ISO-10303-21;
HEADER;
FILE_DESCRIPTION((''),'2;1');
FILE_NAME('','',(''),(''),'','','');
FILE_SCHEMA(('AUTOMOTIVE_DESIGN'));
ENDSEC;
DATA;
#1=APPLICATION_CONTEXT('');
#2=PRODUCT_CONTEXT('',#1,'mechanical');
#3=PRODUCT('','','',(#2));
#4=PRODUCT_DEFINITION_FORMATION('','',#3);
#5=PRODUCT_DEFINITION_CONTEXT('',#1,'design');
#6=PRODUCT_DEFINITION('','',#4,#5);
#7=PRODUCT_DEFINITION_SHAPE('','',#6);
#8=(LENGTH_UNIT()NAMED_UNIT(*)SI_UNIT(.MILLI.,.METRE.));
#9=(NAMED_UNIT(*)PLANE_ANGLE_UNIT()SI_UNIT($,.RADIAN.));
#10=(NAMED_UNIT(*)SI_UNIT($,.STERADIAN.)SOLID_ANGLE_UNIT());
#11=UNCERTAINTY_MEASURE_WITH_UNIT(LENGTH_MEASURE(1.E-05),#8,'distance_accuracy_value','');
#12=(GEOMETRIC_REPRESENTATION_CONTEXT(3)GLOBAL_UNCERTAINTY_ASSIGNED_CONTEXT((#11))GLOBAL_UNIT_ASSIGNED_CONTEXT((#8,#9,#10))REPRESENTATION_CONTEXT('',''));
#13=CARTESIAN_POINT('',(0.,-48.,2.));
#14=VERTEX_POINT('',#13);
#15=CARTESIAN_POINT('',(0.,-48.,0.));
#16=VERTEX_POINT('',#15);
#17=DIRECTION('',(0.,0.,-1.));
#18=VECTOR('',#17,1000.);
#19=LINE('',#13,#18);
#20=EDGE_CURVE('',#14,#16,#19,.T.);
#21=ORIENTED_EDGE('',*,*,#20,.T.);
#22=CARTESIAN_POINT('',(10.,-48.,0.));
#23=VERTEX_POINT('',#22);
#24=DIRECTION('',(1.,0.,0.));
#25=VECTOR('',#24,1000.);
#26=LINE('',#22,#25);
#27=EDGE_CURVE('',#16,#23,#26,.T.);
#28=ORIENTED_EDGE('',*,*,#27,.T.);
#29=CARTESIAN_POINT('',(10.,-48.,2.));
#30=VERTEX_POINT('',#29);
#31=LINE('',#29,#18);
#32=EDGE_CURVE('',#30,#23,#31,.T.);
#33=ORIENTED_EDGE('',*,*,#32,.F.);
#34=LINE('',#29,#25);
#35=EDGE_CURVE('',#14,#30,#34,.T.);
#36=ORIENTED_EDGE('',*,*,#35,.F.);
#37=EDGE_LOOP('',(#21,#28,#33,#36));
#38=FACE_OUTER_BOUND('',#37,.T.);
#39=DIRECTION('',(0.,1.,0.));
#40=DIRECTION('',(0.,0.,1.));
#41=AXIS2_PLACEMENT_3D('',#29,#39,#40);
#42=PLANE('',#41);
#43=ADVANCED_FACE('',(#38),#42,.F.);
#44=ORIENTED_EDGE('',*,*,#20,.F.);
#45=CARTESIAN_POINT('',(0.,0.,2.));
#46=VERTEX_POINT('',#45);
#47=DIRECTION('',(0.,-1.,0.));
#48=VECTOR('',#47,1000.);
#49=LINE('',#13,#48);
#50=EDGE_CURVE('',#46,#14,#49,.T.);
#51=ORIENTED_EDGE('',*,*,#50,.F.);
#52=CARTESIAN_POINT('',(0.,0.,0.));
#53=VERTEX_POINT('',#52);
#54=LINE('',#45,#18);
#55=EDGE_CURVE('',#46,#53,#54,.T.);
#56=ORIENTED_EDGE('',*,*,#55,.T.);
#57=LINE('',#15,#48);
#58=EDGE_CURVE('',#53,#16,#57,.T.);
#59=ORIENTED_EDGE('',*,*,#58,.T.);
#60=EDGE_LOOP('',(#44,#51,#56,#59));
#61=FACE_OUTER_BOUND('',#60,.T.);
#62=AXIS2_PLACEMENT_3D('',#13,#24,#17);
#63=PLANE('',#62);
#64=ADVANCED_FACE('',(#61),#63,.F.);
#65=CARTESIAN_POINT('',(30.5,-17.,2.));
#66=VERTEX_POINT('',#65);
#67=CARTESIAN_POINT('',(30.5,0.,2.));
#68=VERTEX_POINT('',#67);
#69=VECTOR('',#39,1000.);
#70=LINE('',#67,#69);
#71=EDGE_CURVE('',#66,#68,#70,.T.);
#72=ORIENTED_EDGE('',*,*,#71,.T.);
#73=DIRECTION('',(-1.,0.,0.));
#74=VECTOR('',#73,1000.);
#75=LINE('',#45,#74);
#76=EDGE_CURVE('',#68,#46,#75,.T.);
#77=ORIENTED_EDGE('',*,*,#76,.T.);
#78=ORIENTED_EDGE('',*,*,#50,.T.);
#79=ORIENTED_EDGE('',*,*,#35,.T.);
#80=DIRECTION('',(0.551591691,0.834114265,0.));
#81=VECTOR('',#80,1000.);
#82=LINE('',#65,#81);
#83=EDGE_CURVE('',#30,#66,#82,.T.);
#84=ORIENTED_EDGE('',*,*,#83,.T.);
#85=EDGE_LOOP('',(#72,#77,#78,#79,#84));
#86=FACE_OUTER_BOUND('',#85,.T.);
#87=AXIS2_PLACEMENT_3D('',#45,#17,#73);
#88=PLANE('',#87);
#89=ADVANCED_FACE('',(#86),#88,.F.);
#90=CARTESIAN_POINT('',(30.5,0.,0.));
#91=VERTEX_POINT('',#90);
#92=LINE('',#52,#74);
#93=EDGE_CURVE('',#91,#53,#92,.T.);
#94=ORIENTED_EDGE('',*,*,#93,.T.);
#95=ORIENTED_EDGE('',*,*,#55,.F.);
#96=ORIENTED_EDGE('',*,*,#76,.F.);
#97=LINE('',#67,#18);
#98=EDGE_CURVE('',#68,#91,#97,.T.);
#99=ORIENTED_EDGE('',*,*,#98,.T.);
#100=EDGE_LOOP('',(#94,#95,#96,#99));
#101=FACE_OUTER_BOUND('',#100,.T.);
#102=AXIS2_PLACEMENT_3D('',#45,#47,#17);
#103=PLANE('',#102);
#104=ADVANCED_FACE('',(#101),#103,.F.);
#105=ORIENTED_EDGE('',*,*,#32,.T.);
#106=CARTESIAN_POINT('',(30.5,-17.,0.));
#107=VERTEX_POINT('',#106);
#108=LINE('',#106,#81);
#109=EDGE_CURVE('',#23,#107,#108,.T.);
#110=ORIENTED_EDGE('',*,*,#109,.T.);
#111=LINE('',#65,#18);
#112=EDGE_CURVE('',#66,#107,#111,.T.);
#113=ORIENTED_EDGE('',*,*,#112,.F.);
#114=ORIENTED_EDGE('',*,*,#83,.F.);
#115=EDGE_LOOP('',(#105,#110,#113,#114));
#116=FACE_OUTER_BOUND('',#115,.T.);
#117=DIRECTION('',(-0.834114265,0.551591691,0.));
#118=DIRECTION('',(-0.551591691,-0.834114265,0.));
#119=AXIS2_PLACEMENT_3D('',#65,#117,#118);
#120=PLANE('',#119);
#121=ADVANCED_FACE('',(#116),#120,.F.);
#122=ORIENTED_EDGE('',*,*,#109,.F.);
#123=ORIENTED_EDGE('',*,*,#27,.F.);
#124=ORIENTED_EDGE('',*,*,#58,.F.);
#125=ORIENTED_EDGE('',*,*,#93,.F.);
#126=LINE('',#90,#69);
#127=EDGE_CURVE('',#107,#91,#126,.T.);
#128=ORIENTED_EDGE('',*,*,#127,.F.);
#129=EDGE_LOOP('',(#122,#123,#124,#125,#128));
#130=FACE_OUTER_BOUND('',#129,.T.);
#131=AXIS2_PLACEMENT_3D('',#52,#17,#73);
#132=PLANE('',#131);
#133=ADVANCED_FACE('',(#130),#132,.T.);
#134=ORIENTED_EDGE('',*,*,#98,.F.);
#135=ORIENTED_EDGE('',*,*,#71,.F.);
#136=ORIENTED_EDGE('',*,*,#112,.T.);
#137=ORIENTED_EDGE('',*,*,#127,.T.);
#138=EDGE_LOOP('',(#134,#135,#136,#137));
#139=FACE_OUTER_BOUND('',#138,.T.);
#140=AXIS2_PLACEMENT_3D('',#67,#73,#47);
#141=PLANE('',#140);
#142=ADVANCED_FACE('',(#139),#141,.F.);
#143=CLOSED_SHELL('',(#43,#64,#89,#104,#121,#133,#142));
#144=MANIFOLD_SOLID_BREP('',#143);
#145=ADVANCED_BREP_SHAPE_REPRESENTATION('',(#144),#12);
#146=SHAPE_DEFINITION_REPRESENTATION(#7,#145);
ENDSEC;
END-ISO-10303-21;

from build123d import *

# Parameters (mm, degrees)
EXTRUDE_1_DEPTH = 2


with BuildPart() as part:
    # 草图1 → 凸台-拉伸1 (new body)
    with BuildSketch(Plane.XY):
        Polygon((0, 0), (30.5, 0), (30.5, -17), (10, -48), (0, -48), align=None)
    extrude(amount=EXTRUDE_1_DEPTH)


solid = part.part
